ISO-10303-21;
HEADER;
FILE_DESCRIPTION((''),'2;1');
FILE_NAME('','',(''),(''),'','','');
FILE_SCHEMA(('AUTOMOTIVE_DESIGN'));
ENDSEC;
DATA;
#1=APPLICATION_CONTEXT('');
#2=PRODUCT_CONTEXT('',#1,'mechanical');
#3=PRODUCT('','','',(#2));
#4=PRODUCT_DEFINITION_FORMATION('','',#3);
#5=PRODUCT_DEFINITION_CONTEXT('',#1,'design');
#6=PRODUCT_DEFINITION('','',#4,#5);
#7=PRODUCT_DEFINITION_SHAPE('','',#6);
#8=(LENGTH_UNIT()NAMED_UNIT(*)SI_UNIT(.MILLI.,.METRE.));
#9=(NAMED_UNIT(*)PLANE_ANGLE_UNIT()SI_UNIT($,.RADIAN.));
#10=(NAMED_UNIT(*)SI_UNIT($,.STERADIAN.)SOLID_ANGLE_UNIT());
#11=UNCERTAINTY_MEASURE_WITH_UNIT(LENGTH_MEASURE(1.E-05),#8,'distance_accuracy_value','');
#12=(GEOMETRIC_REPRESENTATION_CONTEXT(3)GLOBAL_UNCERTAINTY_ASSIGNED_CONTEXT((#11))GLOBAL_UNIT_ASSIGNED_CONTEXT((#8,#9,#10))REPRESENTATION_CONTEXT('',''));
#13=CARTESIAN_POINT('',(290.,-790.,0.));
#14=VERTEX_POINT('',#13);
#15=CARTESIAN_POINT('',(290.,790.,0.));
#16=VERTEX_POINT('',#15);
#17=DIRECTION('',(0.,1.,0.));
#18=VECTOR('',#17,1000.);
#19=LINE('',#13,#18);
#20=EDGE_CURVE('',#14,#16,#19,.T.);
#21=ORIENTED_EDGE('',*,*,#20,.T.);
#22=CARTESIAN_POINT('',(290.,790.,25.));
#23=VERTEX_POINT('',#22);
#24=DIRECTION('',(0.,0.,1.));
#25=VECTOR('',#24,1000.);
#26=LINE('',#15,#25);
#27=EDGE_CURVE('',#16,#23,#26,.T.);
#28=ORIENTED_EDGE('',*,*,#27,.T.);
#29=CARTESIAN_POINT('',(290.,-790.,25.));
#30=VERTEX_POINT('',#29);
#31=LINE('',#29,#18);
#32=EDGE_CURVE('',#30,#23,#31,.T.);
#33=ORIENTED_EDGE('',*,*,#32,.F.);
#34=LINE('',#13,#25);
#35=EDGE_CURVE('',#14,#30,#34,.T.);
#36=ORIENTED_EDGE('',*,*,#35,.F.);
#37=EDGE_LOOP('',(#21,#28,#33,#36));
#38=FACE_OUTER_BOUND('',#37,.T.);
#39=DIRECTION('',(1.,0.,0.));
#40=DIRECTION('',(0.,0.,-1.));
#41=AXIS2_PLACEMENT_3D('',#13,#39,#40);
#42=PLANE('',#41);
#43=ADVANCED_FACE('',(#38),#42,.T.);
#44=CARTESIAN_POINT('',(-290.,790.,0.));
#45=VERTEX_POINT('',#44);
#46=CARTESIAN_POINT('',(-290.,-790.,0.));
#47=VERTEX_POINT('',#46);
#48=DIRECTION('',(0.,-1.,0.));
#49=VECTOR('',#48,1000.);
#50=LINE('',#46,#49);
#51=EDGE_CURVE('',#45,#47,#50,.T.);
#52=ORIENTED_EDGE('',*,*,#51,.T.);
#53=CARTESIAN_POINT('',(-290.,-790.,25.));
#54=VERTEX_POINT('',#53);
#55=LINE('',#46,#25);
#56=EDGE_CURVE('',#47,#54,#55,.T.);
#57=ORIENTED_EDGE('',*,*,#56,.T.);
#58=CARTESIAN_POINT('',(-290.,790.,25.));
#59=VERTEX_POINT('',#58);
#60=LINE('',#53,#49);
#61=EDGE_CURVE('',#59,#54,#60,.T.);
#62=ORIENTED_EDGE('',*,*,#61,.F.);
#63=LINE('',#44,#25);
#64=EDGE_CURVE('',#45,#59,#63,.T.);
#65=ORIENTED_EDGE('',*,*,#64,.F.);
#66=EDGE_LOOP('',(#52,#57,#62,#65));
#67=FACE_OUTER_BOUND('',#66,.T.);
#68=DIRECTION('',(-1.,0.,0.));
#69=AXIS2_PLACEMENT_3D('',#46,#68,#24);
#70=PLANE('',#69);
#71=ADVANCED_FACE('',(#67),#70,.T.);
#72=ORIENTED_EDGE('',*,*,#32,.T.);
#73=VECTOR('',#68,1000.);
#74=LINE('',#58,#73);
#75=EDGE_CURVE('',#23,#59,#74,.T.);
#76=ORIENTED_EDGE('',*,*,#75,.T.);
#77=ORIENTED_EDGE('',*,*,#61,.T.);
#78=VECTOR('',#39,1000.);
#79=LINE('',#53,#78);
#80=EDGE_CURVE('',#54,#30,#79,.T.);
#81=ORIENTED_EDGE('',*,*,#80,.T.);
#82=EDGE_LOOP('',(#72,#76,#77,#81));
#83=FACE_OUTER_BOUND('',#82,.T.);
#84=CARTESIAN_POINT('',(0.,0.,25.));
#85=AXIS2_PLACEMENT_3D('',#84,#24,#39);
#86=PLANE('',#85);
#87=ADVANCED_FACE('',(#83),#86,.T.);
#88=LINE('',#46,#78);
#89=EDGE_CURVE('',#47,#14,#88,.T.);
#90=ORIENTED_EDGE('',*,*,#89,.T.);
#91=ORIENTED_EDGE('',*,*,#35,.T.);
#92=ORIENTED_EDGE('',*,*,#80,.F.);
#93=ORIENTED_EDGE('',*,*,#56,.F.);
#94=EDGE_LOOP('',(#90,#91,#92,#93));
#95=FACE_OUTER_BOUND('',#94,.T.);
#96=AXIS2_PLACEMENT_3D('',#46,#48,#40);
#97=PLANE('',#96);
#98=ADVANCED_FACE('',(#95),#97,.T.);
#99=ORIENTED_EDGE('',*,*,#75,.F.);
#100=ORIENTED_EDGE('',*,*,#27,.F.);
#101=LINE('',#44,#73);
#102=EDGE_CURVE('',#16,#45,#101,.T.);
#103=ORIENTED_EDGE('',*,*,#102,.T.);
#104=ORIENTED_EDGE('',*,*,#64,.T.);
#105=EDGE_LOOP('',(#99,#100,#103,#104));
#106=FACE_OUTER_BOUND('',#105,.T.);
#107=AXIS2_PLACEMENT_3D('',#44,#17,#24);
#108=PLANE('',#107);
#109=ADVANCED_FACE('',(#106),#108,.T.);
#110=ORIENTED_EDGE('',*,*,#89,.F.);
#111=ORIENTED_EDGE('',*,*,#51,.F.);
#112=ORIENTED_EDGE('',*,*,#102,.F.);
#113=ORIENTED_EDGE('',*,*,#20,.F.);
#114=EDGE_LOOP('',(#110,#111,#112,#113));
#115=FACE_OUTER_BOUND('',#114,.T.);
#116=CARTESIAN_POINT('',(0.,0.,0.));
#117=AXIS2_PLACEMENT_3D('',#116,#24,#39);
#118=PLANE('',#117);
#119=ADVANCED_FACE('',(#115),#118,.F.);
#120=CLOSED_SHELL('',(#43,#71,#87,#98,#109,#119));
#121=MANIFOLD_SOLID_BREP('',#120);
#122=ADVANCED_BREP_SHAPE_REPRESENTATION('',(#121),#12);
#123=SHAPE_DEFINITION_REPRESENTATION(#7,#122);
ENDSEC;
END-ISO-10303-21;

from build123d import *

# Parameters (mm, degrees)
SKETCH_1_W           = 820
SKETCH_1_H           = 1820
EXTRUDE_1_DEPTH      = 25
SKETCH_2_OUTSIDE_W   = 1221.27
SKETCH_2_OUTSIDE_H   = 2221.27
SKETCH_2_OUTSIDE_W_2 = 580
SKETCH_2_OUTSIDE_H_2 = 1580
CUT_EXTRUDE_1_DEPTH  = 999.411237918


with BuildPart() as part:
    # 草图1 → 凸台-拉伸1 (new body)
    with BuildSketch(Plane.XY):
        Rectangle(SKETCH_1_W, SKETCH_1_H)
    extrude(amount=EXTRUDE_1_DEPTH)

    # 草图2 outside → 切除-拉伸1 (cut, through all)
    with BuildSketch(Plane.XY.offset(25)):
        Rectangle(SKETCH_2_OUTSIDE_W, SKETCH_2_OUTSIDE_H)
        Rectangle(SKETCH_2_OUTSIDE_W_2, SKETCH_2_OUTSIDE_H_2, mode=Mode.SUBTRACT)
    extrude(amount=-CUT_EXTRUDE_1_DEPTH, mode=Mode.SUBTRACT)


solid = part.part
